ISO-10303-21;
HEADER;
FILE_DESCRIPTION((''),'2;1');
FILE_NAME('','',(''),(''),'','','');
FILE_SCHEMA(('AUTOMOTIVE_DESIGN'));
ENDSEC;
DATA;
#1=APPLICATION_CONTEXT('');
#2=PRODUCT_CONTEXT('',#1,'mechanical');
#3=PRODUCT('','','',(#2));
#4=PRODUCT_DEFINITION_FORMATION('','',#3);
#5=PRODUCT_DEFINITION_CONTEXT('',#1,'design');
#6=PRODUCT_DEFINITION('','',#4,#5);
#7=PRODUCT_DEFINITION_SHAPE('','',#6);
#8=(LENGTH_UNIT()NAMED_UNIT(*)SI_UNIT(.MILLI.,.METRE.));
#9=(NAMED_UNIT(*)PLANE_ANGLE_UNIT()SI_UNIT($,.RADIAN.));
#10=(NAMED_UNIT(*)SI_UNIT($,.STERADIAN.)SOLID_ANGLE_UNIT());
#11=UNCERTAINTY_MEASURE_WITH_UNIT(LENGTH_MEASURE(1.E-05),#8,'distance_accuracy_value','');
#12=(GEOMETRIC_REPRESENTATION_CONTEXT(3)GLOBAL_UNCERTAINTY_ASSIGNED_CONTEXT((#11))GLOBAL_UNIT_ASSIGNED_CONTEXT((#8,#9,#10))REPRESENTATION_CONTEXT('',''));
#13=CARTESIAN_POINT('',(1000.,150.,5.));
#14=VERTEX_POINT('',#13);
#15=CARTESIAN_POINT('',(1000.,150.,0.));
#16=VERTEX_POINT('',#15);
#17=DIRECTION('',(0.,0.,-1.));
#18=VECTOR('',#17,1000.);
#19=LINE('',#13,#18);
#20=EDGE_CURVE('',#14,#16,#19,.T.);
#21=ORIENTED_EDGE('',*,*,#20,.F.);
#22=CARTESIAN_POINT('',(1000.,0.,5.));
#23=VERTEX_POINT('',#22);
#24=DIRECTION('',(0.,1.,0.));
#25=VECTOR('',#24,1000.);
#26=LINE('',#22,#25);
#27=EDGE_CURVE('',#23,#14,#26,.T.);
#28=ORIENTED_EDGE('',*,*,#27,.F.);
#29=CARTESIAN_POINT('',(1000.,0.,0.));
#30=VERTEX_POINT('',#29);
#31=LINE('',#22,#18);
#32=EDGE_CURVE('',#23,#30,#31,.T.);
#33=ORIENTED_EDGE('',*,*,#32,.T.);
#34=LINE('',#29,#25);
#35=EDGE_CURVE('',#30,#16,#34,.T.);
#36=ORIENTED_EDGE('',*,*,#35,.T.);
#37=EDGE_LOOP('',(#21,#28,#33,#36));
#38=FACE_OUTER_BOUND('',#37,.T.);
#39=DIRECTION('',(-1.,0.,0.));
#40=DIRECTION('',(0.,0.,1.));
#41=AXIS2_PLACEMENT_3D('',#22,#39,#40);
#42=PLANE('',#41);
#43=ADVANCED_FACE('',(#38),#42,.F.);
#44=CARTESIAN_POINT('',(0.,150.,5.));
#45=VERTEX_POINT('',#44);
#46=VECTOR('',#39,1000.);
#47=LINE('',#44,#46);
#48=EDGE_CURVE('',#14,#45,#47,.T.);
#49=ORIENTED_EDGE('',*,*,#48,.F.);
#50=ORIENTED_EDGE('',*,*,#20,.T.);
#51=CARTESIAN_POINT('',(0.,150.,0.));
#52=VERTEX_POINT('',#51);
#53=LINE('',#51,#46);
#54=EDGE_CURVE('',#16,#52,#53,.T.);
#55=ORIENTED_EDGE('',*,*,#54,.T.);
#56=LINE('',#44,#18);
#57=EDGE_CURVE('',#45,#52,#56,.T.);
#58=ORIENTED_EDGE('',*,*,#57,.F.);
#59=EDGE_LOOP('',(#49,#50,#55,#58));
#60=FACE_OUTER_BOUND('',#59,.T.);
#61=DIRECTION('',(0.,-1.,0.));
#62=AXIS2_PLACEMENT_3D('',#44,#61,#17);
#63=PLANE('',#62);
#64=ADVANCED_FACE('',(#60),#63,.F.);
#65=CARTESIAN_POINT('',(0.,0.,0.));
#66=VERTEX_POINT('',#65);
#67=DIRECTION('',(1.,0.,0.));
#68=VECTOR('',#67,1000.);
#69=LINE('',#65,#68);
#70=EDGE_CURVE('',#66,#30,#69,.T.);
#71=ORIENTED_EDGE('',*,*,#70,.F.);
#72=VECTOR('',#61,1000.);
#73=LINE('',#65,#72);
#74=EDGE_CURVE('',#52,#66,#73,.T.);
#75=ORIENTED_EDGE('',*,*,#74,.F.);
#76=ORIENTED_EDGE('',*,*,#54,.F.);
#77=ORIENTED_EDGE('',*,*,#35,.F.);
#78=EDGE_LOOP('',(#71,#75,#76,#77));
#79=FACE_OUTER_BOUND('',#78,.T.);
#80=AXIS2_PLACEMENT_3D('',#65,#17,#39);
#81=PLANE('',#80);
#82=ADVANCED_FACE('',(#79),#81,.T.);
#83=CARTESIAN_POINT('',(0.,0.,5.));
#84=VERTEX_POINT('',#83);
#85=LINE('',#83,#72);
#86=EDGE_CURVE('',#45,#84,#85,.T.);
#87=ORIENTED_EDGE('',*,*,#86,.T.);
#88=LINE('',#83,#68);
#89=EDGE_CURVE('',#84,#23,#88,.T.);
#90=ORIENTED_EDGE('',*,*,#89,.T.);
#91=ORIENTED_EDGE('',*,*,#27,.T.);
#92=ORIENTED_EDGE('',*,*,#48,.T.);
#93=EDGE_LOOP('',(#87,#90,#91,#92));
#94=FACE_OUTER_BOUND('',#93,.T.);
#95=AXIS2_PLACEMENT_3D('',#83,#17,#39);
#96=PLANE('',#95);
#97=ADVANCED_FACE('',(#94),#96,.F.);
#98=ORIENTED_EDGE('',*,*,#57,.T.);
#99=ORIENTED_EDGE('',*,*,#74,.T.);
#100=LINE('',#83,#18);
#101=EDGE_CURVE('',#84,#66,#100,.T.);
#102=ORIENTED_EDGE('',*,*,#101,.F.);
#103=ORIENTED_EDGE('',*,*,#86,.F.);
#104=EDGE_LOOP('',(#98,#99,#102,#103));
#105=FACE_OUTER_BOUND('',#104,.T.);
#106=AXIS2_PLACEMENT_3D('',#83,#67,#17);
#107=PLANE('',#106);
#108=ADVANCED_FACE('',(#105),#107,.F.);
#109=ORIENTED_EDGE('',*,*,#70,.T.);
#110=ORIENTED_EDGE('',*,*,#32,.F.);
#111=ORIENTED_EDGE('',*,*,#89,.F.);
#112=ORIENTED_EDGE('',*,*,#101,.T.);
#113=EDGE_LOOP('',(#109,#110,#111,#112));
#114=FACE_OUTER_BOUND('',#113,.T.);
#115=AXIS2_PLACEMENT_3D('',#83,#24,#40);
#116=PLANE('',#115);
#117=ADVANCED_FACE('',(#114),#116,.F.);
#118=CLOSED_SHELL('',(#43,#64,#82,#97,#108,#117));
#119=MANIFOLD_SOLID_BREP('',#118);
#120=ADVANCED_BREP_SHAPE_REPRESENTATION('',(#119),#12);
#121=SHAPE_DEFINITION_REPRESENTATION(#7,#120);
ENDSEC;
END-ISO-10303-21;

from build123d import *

# Parameters (mm, degrees)
SKETCH1_W           = 1000
SKETCH1_H           = 150
BOSS_EXTRUDE1_DEPTH = 5


with BuildPart() as part:
    # Sketch1 → Boss-Extrude1 (new body)
    with BuildSketch(Plane.XY):
        with Locations((500, 75)):
            Rectangle(SKETCH1_W, SKETCH1_H)
    extrude(amount=BOSS_EXTRUDE1_DEPTH)


solid = part.part
